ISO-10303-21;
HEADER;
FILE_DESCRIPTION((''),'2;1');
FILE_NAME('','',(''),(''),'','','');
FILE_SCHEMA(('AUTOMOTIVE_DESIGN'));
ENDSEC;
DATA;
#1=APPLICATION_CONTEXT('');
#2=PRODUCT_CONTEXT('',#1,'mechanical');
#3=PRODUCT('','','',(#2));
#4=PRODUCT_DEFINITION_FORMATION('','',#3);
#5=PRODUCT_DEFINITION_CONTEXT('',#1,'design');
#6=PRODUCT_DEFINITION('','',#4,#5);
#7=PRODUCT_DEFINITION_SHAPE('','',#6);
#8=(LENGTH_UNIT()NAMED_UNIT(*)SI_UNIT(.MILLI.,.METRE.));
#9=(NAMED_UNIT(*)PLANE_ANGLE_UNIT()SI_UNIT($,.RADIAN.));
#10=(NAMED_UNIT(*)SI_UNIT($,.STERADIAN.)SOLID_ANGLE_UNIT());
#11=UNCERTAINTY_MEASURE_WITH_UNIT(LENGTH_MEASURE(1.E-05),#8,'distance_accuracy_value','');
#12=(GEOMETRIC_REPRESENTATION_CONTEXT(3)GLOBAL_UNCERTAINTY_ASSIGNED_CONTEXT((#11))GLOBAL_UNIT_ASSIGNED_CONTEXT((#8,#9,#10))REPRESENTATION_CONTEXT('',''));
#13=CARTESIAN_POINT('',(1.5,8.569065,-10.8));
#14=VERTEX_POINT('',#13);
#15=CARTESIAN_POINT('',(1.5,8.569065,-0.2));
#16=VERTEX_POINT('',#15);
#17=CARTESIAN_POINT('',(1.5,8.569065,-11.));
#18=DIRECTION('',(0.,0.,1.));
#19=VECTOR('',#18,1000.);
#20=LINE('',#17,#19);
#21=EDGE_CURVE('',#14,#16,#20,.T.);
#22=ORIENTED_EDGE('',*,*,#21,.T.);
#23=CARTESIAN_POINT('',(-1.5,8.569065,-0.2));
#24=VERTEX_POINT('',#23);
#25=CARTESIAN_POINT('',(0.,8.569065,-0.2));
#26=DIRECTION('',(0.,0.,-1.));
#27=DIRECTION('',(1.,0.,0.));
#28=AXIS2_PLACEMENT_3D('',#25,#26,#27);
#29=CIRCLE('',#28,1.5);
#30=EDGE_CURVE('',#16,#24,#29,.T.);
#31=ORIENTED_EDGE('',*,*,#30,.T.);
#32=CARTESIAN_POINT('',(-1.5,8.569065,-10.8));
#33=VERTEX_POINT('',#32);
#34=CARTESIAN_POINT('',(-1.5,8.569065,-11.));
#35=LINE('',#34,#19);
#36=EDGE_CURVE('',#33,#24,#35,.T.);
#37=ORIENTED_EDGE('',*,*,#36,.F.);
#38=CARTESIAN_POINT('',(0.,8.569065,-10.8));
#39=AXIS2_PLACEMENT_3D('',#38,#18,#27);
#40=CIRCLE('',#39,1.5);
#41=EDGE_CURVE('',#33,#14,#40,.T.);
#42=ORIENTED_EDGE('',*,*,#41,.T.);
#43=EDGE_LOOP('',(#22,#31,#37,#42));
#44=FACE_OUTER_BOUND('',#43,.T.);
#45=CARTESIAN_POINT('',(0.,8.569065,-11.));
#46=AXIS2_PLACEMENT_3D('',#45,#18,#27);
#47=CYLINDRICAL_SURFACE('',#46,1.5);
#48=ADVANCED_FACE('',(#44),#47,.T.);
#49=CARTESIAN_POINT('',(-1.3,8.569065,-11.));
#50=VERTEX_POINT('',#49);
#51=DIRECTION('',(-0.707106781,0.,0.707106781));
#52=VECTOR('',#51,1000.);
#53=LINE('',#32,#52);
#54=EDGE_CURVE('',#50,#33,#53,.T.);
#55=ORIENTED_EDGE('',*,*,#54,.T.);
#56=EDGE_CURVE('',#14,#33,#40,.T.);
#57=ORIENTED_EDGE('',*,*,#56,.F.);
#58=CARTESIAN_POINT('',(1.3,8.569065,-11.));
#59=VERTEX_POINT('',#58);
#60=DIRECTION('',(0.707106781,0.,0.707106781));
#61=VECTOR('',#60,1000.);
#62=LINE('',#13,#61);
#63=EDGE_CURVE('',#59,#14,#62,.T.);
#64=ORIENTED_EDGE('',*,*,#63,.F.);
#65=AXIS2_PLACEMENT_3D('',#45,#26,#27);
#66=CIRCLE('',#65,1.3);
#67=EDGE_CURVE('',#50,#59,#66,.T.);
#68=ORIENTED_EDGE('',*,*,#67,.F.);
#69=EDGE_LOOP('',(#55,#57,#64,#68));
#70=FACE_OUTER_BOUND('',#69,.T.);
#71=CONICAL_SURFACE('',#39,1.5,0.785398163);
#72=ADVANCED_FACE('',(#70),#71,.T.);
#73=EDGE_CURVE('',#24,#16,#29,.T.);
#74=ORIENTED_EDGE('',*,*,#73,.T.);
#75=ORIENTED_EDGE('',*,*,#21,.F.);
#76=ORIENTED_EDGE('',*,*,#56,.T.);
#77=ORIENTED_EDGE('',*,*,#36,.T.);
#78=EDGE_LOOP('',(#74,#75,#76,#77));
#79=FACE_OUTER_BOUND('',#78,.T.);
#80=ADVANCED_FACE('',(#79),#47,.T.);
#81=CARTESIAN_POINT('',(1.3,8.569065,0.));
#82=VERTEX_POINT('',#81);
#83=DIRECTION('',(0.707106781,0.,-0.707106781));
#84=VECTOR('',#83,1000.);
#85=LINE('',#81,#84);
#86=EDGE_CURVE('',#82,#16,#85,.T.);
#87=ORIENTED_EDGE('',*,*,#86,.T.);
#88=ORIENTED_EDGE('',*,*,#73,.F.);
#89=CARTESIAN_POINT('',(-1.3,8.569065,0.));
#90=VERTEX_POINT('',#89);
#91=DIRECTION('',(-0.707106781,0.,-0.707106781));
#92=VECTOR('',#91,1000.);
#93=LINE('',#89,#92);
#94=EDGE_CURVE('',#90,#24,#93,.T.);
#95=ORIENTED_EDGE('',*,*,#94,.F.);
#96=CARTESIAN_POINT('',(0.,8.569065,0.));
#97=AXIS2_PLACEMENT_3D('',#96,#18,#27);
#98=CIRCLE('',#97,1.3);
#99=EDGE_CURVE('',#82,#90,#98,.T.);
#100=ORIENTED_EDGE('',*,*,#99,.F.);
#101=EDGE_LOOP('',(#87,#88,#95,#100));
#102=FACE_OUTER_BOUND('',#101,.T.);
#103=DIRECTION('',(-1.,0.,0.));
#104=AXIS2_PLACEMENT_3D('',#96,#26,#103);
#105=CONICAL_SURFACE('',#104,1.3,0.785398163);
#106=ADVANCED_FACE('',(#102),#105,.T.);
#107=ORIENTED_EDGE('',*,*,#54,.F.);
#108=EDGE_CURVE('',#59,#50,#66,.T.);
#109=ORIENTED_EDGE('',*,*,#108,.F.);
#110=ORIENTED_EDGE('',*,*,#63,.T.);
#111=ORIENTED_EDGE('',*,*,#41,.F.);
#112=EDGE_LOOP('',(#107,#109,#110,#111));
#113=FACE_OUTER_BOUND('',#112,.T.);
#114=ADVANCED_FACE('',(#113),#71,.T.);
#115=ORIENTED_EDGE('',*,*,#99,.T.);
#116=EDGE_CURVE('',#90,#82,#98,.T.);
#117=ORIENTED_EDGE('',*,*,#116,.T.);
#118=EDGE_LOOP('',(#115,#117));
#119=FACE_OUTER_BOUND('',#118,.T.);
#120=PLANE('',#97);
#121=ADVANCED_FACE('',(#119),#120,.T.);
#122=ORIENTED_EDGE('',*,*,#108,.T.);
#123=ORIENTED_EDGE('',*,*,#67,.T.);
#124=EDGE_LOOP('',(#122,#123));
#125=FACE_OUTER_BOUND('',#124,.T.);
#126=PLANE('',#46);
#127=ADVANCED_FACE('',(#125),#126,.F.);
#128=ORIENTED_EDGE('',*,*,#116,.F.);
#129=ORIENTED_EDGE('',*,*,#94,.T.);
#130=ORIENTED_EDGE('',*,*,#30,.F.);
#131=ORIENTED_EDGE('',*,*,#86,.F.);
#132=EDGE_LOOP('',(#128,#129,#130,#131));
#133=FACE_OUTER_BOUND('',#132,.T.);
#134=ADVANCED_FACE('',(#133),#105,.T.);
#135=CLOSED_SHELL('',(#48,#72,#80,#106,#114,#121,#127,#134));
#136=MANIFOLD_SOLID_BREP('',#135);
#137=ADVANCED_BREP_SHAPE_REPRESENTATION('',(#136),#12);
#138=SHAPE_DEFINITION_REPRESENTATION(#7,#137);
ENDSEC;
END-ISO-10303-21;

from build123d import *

# Parameters (mm, degrees)
SKETCH1_R           = 1.5
BOSS_EXTRUDE1_DEPTH = 11
CHAMFER1_SIZE       = 0.2


with BuildPart() as part:
    # Sketch1 → Boss-Extrude1 (new body)
    with BuildSketch(Plane.XY):
        with Locations((0, 8.569064594)):
            Circle(SKETCH1_R)
    extrude(amount=-BOSS_EXTRUDE1_DEPTH)

    # Chamfer1
    chamfer1_edges = [part.edges().sort_by_distance(p)[0] for p in [
        (-1.5, 8.569064594, 0),
        (-1.5, 8.569064594, -11),
    ]]
    chamfer(chamfer1_edges, length=CHAMFER1_SIZE)


solid = part.part
